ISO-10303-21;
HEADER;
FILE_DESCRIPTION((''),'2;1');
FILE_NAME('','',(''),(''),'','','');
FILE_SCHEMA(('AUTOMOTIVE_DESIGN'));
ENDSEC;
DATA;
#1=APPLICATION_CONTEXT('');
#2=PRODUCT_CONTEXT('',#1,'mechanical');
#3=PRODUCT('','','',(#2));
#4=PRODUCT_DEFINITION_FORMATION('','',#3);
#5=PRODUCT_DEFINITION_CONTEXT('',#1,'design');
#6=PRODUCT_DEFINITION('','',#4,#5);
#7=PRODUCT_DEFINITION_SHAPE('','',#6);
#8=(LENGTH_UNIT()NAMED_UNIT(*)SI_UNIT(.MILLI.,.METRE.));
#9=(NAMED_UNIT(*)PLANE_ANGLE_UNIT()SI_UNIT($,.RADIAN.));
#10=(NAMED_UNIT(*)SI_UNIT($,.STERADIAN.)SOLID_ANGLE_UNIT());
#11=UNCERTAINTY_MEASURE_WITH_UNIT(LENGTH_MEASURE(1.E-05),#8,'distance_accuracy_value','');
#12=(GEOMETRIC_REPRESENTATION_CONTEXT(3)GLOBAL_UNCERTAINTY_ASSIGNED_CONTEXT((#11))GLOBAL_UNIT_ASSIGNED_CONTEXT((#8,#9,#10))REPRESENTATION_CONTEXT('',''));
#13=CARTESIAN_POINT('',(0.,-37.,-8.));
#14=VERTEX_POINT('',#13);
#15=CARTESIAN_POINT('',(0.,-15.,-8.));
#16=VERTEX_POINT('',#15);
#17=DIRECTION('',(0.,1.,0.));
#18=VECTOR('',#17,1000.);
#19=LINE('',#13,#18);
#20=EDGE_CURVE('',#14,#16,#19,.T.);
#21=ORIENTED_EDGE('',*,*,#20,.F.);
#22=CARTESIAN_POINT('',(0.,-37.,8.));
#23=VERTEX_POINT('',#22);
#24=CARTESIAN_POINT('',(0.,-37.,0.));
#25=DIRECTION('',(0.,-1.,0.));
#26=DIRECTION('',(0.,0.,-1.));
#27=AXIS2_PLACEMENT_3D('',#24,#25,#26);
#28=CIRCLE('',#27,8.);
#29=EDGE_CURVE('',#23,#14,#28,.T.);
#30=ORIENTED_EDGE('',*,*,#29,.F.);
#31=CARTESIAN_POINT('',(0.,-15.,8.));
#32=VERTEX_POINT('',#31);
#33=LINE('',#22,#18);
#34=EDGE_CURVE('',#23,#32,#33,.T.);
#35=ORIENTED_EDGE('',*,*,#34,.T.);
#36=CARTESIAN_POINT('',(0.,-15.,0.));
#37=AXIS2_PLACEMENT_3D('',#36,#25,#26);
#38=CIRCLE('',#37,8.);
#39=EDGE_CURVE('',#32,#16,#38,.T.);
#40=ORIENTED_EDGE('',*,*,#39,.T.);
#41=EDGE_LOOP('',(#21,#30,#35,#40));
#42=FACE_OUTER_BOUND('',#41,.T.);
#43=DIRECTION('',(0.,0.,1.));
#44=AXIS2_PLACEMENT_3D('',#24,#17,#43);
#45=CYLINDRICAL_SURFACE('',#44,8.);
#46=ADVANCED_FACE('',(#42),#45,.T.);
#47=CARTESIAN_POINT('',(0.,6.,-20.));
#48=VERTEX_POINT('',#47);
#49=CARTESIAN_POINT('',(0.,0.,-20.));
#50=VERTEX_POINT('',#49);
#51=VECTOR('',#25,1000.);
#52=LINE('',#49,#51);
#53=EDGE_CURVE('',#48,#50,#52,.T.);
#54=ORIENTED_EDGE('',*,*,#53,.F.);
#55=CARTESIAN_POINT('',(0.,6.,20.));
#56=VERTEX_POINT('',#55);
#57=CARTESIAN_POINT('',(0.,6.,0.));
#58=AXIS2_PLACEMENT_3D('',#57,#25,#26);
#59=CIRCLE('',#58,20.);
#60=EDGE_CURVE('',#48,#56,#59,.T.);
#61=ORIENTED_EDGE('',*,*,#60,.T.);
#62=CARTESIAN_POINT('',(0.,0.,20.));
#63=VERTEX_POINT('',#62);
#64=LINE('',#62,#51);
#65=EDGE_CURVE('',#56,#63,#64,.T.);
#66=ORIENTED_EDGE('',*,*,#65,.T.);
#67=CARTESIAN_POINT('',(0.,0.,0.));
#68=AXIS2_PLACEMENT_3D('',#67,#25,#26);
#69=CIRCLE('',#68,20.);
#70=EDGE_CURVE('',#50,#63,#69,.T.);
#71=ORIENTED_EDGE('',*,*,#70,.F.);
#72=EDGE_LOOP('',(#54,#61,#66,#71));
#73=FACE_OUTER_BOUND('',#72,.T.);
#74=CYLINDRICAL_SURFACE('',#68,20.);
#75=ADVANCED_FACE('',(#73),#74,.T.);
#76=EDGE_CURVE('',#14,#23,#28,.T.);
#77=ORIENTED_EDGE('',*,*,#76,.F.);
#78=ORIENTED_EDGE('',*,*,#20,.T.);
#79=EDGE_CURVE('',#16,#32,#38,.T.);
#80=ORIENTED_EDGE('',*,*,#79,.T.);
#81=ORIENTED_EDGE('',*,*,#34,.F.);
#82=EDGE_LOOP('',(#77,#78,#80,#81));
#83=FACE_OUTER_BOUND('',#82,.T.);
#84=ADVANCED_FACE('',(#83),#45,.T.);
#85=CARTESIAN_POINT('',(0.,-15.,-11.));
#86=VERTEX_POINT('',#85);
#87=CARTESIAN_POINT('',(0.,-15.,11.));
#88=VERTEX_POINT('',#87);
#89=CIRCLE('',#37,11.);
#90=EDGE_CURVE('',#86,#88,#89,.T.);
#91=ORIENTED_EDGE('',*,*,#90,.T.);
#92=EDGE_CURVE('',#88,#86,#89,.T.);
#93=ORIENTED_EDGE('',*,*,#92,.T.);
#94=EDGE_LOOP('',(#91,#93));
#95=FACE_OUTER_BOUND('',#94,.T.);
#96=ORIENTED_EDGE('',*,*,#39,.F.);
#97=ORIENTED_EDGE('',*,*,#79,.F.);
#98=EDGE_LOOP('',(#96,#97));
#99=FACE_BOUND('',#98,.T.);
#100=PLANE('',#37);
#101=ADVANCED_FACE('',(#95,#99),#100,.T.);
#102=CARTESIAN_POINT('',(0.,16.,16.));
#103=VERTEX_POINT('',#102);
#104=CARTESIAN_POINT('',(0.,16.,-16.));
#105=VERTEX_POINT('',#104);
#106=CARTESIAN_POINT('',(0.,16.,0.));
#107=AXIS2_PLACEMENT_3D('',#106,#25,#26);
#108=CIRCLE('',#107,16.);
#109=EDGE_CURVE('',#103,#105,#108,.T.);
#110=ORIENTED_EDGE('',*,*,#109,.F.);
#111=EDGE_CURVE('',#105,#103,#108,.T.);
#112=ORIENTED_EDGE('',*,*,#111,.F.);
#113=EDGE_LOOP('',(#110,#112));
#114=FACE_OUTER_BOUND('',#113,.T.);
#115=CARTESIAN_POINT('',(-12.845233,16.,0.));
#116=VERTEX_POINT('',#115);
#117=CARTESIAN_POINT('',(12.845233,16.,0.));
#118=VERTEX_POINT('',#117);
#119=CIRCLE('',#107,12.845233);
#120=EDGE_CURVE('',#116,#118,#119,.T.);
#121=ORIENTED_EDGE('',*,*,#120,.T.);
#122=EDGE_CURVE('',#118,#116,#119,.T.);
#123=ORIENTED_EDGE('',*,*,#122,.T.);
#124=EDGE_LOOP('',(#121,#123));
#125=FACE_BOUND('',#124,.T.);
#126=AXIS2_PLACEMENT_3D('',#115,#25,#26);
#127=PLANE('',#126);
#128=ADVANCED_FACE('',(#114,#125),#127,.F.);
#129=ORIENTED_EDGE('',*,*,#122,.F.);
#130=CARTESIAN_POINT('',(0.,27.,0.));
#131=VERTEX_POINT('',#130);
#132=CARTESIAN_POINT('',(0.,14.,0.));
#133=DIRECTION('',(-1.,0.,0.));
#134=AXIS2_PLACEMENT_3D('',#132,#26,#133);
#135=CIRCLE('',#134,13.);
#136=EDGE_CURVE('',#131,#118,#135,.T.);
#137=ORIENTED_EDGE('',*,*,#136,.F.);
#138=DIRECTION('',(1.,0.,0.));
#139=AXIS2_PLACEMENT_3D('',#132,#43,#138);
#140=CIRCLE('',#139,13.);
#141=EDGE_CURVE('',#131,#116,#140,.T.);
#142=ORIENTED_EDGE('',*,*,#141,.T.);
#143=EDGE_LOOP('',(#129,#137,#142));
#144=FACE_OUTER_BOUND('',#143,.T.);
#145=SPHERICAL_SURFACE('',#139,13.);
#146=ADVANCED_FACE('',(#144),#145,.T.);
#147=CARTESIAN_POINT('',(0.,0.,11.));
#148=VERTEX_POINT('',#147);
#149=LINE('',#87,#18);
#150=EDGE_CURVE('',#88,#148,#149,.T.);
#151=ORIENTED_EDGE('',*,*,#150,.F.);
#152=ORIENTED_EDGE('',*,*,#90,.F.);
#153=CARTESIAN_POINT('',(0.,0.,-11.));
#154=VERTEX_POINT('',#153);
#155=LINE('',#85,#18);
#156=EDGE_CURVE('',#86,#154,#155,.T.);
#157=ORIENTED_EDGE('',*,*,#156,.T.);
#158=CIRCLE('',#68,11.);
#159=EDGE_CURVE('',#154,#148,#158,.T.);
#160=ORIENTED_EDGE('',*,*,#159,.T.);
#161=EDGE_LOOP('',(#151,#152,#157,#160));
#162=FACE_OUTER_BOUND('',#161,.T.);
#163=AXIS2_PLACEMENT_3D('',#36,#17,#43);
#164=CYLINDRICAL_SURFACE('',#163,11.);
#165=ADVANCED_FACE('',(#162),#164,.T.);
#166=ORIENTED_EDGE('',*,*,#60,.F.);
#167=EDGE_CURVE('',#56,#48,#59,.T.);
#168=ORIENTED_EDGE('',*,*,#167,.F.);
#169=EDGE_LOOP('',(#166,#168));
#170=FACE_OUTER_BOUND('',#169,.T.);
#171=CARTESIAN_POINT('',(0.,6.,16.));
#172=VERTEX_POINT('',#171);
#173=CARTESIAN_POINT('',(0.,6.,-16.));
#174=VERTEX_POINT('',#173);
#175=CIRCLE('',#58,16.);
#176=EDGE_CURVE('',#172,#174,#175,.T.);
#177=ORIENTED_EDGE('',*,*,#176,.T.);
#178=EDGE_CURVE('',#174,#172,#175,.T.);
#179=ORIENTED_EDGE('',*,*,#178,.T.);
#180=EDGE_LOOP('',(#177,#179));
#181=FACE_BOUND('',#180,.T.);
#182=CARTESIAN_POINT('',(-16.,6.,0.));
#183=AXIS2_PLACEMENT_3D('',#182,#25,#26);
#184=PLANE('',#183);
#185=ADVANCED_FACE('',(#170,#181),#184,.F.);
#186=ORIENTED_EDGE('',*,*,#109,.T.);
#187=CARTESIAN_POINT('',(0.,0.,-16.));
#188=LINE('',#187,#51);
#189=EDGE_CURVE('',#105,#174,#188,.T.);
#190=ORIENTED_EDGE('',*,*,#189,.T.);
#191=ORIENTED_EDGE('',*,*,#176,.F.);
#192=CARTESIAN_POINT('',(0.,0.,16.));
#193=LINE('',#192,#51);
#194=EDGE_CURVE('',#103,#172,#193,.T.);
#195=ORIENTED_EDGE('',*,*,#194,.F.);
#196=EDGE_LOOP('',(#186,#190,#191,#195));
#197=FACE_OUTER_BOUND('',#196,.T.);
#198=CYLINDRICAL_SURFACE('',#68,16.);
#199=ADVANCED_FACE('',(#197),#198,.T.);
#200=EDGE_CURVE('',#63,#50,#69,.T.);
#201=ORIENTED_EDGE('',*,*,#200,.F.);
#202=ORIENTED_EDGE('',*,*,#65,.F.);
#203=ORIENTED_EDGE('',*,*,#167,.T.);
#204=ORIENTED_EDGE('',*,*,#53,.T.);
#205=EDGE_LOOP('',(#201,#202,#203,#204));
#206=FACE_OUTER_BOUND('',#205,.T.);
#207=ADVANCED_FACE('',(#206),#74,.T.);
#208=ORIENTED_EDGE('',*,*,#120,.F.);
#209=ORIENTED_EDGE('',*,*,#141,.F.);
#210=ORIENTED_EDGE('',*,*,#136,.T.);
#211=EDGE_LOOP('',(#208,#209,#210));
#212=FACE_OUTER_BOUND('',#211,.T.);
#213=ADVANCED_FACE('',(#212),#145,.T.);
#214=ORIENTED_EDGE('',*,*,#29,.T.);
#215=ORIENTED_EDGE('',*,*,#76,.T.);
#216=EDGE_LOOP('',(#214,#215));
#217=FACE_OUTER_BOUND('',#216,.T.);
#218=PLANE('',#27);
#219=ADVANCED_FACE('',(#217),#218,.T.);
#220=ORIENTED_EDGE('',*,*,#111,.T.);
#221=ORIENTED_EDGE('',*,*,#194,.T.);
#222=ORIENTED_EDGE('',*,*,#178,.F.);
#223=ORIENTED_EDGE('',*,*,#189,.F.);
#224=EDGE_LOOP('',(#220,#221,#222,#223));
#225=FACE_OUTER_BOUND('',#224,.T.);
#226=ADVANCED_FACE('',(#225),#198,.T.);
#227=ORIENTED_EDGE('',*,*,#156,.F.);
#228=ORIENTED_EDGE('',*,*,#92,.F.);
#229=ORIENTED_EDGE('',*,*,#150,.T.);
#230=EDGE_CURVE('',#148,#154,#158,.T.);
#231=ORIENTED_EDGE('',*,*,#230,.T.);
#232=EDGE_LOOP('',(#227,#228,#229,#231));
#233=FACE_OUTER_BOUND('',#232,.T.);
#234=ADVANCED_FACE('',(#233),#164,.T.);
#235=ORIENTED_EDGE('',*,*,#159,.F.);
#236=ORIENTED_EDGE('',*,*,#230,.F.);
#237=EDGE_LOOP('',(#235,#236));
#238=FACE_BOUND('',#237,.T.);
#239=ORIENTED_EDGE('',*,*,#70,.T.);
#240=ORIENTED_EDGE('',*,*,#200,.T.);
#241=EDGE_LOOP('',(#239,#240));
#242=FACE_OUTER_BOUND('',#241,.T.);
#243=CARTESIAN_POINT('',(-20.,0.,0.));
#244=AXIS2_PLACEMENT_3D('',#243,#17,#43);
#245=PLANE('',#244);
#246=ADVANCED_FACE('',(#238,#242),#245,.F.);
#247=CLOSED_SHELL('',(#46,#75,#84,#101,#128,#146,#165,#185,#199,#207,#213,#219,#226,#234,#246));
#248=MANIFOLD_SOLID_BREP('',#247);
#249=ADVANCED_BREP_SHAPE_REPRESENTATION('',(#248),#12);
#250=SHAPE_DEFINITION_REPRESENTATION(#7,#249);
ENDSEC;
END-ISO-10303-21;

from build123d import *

# Parameters (mm, degrees)
SKETCH2_R           = 11
BOSS_EXTRUDE1_DEPTH = 15
SKETCH3_R           = 8
BOSS_EXTRUDE2_DEPTH = 22


with BuildPart() as part:
    # Sketch1 → Revolve1 (revolve)
    with BuildSketch(Plane.XY, mode=Mode.PRIVATE) as revolve1_sk:
        with BuildLine():
            Line((-12.845232579, 16), (-16, 16))
            Line((-16, 16), (-16, 6))
            Line((-16, 6), (-20, 6))
            Line((-20, 6), (-20, 0))
            Line((-20, 0), (0, 0))
            Line((0, 0), (0, 27))
            ThreePointArc((0, 27), (-8.455767263, 23.874208829), (-12.845232579, 16))
        make_face()
    revolve(revolve1_sk.sketch.rotate(Axis((0, 0, 0), (0, 1, 0)), 270), axis=Axis((0, 0, 0), (0, 1, 0)))

    # Sketch2 → Boss-Extrude1 (add)
    with BuildSketch(Plane(origin=(0, 0, 0), x_dir=(-1, 0, 0), z_dir=(0, -1, 0))):
        with Locations(Location((0, 0, 0), (0, 0, 90))):
            Circle(SKETCH2_R)
    extrude(amount=BOSS_EXTRUDE1_DEPTH)

    # Sketch3 → Boss-Extrude2 (add)
    with BuildSketch(Plane(origin=(0, -15, 0), x_dir=(-1, 0, 0), z_dir=(0, -1, 0))):
        with Locations(Location((0, 0, 0), (0, 0, 90))):
            Circle(SKETCH3_R)
    extrude(amount=BOSS_EXTRUDE2_DEPTH)


solid = part.part
